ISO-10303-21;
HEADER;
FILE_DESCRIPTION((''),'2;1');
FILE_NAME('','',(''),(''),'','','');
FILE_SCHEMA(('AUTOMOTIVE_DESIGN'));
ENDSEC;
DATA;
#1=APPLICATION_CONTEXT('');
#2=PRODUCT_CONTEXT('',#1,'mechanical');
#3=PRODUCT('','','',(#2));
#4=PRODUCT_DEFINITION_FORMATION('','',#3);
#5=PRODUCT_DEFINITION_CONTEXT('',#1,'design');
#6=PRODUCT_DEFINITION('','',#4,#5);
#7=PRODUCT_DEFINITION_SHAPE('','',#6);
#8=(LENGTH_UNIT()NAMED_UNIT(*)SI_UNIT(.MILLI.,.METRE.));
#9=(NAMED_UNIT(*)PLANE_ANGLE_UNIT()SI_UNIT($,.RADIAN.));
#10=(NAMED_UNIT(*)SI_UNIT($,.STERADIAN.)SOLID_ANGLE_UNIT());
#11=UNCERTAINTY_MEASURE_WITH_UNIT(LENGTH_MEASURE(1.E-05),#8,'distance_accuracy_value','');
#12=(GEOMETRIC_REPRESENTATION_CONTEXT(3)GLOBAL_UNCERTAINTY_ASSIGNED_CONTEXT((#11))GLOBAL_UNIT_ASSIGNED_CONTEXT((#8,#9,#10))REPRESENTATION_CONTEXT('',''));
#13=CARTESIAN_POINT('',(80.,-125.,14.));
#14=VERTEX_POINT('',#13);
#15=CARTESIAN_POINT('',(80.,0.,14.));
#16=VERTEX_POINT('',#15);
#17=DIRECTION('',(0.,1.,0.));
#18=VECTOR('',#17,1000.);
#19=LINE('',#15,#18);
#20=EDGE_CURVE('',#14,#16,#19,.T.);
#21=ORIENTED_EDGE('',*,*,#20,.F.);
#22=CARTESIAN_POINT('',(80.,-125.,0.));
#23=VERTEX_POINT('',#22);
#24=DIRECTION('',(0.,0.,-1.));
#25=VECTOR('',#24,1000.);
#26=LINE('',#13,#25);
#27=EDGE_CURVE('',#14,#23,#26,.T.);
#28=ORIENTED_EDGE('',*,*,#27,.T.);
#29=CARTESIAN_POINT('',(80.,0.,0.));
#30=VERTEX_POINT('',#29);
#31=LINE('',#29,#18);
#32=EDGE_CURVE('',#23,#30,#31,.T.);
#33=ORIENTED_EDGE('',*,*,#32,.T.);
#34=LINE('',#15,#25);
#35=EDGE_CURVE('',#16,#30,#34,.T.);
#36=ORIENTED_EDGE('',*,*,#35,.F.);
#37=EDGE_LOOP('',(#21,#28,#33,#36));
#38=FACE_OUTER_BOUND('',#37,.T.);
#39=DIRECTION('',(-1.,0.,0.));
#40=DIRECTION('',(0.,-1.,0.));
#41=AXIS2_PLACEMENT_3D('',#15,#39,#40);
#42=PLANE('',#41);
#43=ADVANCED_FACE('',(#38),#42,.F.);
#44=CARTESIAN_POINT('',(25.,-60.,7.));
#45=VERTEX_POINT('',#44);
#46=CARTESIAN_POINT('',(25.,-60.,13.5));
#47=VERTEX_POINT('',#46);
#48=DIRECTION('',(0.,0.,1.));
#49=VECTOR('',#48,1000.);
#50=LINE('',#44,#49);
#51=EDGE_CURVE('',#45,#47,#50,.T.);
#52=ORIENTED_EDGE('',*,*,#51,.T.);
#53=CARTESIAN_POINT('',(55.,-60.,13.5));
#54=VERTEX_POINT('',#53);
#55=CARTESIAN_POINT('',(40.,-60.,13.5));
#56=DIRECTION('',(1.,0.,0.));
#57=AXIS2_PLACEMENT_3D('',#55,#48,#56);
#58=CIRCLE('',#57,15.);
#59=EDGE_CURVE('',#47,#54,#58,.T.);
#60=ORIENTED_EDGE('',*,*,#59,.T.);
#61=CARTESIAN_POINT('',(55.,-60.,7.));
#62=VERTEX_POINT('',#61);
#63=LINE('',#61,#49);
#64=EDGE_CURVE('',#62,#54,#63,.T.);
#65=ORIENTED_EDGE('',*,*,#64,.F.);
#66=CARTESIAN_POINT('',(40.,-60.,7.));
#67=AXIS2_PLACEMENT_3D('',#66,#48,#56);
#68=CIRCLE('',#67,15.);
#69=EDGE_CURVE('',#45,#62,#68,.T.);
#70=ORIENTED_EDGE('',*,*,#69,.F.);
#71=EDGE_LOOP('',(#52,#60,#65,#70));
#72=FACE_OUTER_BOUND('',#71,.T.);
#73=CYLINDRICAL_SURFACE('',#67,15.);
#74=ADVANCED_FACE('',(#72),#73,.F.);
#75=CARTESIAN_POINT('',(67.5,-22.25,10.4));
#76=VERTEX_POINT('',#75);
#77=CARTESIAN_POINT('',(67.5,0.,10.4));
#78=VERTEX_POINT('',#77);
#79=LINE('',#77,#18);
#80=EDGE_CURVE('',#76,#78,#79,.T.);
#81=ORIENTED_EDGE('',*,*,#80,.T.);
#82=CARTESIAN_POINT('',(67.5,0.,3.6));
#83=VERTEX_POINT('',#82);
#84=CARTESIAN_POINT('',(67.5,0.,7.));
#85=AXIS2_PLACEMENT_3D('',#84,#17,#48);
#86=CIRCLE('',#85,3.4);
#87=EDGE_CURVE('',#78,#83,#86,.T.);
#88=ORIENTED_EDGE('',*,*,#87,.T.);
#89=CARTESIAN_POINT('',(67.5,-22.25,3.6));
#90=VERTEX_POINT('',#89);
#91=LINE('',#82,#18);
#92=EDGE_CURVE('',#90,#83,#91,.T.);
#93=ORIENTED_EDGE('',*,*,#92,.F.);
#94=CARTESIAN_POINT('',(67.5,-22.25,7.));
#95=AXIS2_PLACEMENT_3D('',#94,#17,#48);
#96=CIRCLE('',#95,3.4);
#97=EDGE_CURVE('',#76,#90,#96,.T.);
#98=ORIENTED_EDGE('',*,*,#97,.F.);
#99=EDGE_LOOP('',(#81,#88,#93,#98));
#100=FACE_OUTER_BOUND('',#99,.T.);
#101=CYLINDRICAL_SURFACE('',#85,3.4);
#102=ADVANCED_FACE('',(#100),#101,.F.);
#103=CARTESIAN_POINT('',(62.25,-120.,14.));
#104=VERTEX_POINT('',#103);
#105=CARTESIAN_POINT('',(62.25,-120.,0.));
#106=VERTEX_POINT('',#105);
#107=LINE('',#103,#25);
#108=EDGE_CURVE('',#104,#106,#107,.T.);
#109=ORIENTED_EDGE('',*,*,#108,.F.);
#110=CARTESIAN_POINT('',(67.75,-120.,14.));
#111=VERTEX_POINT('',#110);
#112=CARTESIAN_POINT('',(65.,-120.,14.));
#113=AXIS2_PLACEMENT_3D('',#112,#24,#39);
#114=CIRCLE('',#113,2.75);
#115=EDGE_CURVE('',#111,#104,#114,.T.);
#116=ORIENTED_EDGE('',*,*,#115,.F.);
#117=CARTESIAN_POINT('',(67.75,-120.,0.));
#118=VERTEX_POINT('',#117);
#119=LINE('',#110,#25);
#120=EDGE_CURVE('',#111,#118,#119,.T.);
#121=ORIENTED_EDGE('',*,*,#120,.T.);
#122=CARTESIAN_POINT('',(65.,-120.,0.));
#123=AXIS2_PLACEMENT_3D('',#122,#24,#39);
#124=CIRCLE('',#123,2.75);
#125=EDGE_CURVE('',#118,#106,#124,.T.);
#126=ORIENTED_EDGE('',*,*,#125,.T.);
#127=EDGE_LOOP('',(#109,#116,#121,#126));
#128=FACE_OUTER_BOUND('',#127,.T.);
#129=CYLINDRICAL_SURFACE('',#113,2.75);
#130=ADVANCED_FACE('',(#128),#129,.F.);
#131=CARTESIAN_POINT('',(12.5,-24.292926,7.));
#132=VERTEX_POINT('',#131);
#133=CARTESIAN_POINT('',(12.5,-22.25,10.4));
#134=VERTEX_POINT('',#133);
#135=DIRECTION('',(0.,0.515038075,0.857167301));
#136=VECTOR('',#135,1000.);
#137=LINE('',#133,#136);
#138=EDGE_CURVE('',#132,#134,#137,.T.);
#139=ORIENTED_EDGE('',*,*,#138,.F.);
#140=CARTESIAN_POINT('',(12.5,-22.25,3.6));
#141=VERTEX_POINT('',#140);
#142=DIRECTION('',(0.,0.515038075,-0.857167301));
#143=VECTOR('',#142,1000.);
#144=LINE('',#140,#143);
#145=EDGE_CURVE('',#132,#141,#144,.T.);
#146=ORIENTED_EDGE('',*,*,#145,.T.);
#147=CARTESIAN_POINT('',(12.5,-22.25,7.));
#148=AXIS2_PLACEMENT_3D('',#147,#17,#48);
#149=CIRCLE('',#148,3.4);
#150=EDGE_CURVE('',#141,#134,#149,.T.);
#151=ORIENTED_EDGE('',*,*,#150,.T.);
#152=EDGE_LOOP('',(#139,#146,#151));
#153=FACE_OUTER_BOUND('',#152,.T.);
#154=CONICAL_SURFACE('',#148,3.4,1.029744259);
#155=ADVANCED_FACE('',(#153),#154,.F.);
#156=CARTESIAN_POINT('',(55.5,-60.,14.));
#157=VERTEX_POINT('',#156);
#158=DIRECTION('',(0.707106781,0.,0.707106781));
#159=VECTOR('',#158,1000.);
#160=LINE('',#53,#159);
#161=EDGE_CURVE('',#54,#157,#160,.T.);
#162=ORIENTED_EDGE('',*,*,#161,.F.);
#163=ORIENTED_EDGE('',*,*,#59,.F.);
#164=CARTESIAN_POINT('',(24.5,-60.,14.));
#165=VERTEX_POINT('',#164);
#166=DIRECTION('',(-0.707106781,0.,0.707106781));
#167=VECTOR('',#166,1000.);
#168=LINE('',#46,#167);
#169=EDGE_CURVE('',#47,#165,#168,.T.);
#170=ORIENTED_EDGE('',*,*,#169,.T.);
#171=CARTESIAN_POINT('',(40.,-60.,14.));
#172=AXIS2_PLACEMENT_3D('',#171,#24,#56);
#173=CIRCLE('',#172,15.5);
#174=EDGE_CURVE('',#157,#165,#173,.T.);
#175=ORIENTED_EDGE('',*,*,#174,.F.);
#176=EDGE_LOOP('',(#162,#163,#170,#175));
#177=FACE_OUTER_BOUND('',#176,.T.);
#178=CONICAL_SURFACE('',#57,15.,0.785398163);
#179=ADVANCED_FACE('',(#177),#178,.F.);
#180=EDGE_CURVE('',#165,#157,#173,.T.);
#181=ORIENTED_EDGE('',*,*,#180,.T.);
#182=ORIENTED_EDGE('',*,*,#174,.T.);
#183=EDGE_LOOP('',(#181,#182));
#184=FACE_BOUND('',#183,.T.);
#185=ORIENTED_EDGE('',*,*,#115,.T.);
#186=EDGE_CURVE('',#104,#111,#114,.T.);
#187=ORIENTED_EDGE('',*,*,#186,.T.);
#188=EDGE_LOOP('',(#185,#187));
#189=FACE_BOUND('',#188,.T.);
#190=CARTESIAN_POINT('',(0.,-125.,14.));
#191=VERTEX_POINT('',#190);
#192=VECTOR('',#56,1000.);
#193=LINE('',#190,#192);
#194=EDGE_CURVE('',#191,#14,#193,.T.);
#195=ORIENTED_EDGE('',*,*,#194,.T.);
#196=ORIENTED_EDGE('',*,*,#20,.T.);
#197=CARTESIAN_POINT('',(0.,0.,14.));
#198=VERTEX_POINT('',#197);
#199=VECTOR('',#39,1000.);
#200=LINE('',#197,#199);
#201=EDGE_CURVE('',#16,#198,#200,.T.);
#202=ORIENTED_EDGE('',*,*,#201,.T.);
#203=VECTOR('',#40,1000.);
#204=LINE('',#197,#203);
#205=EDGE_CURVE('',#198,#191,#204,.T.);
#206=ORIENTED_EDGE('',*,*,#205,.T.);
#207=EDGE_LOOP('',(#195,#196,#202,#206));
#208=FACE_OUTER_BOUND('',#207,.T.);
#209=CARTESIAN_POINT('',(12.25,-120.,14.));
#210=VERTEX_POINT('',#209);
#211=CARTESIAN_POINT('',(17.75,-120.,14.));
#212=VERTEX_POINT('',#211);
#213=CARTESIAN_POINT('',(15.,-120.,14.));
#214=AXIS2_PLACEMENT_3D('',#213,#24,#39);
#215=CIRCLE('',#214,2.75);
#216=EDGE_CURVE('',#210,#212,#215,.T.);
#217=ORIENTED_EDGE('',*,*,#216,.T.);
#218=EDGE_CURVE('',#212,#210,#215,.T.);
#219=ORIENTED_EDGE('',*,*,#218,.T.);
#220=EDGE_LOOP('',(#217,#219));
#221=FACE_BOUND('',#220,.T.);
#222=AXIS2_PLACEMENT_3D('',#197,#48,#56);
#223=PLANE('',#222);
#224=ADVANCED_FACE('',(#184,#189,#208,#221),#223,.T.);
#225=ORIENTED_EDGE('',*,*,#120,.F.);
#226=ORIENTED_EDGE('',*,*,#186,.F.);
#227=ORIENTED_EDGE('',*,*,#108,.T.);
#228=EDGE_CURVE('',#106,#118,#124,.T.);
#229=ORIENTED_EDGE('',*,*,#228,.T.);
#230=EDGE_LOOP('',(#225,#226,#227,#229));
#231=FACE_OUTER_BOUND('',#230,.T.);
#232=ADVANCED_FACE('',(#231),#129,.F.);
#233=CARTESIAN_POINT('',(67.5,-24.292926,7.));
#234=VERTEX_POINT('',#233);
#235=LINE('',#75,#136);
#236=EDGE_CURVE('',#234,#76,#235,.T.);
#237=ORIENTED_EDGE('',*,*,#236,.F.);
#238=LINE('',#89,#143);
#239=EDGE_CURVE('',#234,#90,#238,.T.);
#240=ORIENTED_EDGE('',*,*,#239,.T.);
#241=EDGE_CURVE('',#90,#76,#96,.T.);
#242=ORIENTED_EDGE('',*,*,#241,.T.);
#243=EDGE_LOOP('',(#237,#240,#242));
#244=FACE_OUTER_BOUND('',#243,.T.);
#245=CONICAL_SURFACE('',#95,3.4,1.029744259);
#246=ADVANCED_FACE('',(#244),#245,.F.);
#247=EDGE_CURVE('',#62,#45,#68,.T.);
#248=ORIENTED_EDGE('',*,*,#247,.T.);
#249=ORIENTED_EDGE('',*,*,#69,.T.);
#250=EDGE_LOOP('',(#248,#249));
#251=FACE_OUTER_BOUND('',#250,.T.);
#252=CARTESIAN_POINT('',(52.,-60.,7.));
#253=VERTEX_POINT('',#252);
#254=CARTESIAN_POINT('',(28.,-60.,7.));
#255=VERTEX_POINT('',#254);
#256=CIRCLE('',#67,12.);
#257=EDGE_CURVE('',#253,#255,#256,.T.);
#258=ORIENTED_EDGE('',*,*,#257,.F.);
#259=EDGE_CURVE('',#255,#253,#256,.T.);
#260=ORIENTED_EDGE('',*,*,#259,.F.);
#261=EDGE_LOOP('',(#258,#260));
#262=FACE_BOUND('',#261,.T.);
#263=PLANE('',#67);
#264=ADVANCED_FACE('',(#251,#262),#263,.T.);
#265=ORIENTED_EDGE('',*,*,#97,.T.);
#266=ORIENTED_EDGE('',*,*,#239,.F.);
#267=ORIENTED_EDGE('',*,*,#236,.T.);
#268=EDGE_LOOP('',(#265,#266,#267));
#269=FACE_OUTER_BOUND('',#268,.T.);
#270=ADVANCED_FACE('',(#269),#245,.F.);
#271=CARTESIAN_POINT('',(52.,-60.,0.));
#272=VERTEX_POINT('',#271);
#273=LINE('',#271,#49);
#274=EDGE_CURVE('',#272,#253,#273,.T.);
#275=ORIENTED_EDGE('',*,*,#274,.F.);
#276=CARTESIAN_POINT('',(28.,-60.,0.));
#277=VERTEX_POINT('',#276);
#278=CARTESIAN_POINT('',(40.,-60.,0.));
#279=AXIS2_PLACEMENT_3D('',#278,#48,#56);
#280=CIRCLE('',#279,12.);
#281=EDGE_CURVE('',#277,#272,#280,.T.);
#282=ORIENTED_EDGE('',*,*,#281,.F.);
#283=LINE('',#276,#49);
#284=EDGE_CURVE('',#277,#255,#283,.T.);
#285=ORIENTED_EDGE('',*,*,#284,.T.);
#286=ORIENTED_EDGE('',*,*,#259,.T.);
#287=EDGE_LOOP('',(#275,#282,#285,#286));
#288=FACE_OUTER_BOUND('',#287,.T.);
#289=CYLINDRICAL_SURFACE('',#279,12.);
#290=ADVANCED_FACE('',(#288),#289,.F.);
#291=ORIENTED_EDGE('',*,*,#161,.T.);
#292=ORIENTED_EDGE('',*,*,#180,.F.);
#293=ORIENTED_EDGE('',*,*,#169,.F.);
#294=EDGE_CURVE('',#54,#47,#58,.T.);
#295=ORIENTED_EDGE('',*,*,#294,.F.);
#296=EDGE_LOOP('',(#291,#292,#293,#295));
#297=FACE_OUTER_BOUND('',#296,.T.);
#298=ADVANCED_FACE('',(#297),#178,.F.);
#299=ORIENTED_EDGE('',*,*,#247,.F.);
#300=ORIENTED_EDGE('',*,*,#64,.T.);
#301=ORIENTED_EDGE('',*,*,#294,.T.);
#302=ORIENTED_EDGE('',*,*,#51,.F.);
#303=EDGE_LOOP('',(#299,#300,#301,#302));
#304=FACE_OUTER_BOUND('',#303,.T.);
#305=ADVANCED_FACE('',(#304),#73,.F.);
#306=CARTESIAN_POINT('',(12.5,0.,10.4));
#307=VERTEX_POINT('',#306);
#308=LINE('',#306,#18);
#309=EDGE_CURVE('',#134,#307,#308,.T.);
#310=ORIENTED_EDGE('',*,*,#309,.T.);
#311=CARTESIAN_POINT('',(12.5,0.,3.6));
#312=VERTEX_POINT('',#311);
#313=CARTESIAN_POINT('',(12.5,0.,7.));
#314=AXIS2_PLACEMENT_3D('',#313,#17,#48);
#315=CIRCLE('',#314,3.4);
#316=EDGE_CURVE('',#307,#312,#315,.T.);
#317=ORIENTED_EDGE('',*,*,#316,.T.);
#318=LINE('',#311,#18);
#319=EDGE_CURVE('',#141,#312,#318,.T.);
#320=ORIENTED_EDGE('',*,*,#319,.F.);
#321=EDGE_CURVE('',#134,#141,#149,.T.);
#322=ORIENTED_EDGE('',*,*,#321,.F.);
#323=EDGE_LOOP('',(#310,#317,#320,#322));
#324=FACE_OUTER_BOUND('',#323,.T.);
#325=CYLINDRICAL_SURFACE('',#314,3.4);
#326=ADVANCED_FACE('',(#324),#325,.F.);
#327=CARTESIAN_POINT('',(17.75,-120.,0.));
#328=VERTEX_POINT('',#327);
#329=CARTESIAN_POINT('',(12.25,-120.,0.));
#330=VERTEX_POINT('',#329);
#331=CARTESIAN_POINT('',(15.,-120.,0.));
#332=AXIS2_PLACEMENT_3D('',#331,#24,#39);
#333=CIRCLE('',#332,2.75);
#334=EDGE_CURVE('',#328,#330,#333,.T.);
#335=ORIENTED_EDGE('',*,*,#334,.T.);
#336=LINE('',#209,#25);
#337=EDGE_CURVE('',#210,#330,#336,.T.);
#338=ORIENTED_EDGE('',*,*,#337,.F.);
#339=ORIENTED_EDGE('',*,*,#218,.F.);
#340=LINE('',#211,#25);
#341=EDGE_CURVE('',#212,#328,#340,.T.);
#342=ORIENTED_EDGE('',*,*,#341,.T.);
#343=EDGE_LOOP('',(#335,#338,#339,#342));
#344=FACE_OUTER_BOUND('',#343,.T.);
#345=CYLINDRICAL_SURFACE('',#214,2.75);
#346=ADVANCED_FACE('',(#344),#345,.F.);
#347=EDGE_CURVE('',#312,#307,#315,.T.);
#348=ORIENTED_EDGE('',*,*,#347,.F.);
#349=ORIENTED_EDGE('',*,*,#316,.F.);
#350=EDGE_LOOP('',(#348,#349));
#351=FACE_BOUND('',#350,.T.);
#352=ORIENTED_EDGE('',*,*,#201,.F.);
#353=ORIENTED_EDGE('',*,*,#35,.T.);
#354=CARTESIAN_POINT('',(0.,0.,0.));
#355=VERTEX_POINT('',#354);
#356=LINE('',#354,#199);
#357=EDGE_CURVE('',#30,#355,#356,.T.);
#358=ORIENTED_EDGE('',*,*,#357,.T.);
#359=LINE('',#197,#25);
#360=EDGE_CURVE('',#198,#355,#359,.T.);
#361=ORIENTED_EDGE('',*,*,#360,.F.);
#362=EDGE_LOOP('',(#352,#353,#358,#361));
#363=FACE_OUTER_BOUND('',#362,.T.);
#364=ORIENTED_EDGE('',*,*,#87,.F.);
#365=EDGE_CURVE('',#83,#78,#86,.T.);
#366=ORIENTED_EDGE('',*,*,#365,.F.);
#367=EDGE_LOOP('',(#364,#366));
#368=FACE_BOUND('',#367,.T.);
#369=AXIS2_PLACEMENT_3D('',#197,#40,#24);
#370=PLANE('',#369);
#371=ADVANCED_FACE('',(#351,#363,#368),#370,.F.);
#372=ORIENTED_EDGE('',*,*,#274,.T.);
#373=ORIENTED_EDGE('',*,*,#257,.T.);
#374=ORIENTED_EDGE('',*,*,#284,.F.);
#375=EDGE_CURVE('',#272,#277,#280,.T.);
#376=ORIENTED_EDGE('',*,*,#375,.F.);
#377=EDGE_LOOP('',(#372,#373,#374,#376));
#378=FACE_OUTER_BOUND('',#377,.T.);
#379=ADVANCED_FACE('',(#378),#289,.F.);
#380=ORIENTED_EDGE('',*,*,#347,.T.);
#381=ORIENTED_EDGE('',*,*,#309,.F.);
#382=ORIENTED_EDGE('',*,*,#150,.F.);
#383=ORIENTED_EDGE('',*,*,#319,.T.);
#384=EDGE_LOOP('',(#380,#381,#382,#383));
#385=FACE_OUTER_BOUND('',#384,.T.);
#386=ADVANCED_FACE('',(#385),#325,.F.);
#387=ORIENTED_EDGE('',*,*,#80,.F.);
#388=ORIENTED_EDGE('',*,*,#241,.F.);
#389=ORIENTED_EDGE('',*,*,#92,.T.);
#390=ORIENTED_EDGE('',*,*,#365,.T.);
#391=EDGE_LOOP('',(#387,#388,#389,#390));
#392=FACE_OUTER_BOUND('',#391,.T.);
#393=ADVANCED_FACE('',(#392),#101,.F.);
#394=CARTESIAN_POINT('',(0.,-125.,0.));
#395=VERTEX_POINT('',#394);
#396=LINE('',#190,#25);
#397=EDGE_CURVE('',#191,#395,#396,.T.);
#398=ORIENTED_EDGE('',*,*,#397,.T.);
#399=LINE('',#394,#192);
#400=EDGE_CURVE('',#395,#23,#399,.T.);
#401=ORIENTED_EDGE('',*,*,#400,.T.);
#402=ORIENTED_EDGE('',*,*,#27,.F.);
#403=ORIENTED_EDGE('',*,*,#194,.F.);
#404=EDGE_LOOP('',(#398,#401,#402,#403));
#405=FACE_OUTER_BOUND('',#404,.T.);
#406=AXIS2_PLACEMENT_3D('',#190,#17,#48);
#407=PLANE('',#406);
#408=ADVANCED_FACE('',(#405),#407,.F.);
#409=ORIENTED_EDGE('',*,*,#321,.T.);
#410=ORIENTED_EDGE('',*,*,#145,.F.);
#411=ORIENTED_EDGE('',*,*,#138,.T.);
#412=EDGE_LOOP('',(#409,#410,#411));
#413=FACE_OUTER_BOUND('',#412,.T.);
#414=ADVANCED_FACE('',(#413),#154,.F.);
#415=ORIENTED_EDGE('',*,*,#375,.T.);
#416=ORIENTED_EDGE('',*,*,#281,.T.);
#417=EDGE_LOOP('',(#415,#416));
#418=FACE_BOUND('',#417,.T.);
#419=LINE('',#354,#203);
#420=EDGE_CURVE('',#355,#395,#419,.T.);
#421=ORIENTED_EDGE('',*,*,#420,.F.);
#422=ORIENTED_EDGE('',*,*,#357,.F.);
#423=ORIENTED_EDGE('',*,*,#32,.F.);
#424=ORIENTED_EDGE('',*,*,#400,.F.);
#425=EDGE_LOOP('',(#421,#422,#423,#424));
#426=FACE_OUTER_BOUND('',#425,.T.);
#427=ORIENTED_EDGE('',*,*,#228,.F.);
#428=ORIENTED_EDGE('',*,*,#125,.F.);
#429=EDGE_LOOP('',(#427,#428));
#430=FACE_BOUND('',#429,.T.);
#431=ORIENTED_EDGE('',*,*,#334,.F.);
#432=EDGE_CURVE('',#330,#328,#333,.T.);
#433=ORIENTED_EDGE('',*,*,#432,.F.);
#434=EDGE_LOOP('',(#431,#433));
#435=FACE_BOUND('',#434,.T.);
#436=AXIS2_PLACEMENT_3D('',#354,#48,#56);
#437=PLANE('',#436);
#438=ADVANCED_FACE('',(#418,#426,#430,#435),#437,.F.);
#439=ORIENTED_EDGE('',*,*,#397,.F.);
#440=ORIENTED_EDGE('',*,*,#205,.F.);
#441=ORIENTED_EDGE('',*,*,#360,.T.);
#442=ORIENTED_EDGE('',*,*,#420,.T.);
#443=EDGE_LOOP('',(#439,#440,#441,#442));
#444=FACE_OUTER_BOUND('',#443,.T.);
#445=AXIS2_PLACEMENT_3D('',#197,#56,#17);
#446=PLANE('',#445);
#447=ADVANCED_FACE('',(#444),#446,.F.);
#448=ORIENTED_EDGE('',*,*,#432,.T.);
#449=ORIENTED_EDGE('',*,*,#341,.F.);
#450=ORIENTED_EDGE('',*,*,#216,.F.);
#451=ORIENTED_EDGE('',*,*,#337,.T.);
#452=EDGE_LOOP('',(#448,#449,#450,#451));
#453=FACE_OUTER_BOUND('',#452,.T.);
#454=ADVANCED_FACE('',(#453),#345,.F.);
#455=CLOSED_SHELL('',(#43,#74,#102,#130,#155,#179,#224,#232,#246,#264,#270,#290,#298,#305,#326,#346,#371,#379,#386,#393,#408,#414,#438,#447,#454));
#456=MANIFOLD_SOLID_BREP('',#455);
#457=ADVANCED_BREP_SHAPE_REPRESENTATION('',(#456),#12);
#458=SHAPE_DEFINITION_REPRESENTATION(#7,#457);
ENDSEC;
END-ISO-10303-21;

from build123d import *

# Parameters (mm, degrees)
SKETCH_1_W             = 80
SKETCH_1_H             = 125
EXTRUDE_1_DEPTH        = 14
SKETCH_2_R             = 15
CUT_EXTRUDE_1_DEPTH    = 7
SKETCH_3_R             = 12
CUT_EXTRUDE_2_DEPTH    = 149.573214275
CHAMFER_2_SIZE         = 0.5
HOLE_WIZARD_M8_1_D     = 6.8
HOLE_WIZARD_M8_1_DEPTH = 22.25
HOLE_WIZARD_M8_1_TIP   = 2.042926105
SKETCH_10_R            = 2.75
CUT_EXTRUDE_3_DEPTH    = 150.067098986


with BuildPart() as part:
    # 草图1 → 凸台-拉伸1 (new body)
    with BuildSketch(Plane.XY):
        with Locations((40, -62.5)):
            Rectangle(SKETCH_1_W, SKETCH_1_H)
    extrude(amount=EXTRUDE_1_DEPTH)

    # 草图2 → 切除-拉伸1 (cut)
    with BuildSketch(Plane.XY.offset(14)):
        with Locations((40, -60)):
            Circle(SKETCH_2_R)
    extrude(amount=-CUT_EXTRUDE_1_DEPTH, mode=Mode.SUBTRACT)

    # 草图3 → 切除-拉伸2 (cut, through all)
    with BuildSketch(Plane.XY.offset(7)):
        with Locations((40, -60)):
            Circle(SKETCH_3_R)
    extrude(amount=-CUT_EXTRUDE_2_DEPTH, mode=Mode.SUBTRACT)

    # 倒角2
    chamfer_2_edges = [part.edges().sort_by_distance(p)[0] for p in [
        (25, -60, 14),
    ]]
    chamfer(chamfer_2_edges, length=CHAMFER_2_SIZE)

    # M8 螺纹孔1
    with Locations(Plane(origin=(0, 0, 0), x_dir=(1, 0, 0), z_dir=(0, 1, 0))):
        with Locations((67.5, -7), (12.5, -7)):
            Hole(HOLE_WIZARD_M8_1_D / 2, depth=HOLE_WIZARD_M8_1_DEPTH)
            with Locations((0, 0, -(HOLE_WIZARD_M8_1_DEPTH + HOLE_WIZARD_M8_1_TIP / 2))):  # 118° drill point
                Cone(0, HOLE_WIZARD_M8_1_D / 2, HOLE_WIZARD_M8_1_TIP, mode=Mode.SUBTRACT)

    # 草图10 → 切除-拉伸3 (cut, through all)
    with BuildSketch(Plane(origin=(0, 0, 0), x_dir=(-1, 0, 0), z_dir=(0, 0, -1))):
        with Locations((-65, -120)):
            Circle(SKETCH_10_R)
        with Locations((-15, -120)):
            Circle(SKETCH_10_R)
    extrude(amount=-CUT_EXTRUDE_3_DEPTH, mode=Mode.SUBTRACT)


solid = part.part
